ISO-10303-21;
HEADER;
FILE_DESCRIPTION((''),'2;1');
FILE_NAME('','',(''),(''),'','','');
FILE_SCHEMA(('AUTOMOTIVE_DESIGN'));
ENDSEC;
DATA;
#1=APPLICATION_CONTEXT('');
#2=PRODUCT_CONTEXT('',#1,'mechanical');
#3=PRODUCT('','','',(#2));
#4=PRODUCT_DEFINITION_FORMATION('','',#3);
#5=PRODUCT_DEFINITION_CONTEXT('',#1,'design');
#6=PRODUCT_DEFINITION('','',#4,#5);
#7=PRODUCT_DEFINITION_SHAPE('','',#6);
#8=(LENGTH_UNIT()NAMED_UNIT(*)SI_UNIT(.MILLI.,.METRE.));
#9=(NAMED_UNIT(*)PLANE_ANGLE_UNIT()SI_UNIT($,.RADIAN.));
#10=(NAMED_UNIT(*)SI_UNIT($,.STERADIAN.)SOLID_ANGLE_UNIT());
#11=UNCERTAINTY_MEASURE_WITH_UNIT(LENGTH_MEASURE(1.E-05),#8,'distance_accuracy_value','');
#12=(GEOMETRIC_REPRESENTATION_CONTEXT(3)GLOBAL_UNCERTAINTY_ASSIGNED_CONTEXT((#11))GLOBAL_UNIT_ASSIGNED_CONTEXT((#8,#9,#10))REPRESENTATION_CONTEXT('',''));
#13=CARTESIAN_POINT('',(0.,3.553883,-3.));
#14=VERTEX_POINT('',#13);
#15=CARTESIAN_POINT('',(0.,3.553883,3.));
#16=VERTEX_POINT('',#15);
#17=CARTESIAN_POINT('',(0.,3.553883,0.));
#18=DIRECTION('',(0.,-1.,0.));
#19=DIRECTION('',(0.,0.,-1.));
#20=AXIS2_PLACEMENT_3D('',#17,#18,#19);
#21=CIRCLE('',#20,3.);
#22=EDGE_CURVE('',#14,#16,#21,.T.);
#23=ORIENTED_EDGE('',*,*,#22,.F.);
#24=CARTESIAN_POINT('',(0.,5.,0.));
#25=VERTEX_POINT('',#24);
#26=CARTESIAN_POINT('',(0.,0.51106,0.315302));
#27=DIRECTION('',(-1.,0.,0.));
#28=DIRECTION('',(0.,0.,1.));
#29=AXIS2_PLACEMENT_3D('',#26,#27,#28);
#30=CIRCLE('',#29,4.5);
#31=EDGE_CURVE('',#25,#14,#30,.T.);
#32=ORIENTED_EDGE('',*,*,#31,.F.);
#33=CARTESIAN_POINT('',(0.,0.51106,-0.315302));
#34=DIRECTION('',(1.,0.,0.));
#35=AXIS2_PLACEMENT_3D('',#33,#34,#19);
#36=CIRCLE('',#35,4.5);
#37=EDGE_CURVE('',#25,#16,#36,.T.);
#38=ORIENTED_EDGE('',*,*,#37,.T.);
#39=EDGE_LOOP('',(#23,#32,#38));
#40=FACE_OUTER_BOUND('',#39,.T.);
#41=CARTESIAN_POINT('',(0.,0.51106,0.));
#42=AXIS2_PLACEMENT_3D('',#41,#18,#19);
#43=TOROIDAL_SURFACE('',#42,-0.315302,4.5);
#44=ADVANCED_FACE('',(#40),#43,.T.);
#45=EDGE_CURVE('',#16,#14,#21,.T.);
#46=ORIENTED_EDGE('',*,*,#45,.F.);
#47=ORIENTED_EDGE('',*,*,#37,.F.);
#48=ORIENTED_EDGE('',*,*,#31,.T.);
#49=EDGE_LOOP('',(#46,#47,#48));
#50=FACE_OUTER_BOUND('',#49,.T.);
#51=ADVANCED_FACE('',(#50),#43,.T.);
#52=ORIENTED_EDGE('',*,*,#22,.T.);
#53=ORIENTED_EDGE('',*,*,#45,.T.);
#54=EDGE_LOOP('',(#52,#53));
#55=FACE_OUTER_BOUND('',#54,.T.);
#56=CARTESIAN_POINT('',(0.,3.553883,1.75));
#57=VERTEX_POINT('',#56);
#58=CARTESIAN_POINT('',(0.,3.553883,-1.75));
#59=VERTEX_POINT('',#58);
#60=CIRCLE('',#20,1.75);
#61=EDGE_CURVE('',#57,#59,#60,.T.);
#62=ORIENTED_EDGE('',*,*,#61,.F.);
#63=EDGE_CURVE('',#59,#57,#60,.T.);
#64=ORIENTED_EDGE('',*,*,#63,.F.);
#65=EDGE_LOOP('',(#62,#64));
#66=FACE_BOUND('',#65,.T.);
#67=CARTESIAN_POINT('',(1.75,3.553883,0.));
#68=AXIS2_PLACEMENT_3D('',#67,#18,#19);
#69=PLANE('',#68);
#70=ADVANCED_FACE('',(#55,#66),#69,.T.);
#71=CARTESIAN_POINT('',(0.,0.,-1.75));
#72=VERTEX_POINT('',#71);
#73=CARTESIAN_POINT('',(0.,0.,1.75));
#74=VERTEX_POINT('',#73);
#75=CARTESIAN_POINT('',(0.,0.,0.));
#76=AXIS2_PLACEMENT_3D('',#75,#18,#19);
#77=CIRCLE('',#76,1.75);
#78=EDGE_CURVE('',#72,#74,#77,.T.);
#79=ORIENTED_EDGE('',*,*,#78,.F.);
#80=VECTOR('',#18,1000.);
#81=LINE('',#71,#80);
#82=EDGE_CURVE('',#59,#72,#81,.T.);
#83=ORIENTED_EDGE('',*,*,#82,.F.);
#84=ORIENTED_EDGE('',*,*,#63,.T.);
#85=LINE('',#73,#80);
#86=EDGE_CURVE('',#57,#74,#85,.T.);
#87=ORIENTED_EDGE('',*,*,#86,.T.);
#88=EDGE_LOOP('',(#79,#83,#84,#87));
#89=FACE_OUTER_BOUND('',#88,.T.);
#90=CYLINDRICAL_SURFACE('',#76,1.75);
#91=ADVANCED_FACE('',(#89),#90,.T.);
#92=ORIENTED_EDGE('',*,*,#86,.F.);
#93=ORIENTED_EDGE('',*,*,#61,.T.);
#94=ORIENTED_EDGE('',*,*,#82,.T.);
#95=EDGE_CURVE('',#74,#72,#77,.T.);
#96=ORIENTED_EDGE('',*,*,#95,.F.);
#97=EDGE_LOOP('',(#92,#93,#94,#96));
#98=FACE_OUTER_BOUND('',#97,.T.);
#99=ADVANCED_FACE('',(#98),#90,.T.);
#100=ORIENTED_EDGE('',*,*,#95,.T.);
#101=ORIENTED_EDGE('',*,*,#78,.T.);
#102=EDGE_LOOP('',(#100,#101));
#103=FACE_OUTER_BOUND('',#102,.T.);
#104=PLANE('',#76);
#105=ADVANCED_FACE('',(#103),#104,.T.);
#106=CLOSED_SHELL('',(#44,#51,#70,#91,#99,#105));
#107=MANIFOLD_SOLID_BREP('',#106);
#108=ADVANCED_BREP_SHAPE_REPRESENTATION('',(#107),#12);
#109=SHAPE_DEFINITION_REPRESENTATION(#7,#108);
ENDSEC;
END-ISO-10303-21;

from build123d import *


with BuildPart() as part:
    # End Cap Half Profile → End Cap Revolve (revolve)
    with BuildSketch(Plane.XY, mode=Mode.PRIVATE) as end_cap_revolve_sk:
        with BuildLine():
            Line((0, 0), (1.75, 0))
            Line((1.75, 0), (1.75, 3.553882595))
            Line((1.75, 3.553882595), (3, 3.553882595))
            ThreePointArc((3, 3.553882595), (1.638702903, 4.564683294), (0, 5))
            Line((0, 5), (0, 0))
        make_face()
    revolve(end_cap_revolve_sk.sketch.rotate(Axis((0, 0, 0), (0, 1, 0)), 90), axis=Axis((0, 0, 0), (0, 1, 0)))


solid = part.part
